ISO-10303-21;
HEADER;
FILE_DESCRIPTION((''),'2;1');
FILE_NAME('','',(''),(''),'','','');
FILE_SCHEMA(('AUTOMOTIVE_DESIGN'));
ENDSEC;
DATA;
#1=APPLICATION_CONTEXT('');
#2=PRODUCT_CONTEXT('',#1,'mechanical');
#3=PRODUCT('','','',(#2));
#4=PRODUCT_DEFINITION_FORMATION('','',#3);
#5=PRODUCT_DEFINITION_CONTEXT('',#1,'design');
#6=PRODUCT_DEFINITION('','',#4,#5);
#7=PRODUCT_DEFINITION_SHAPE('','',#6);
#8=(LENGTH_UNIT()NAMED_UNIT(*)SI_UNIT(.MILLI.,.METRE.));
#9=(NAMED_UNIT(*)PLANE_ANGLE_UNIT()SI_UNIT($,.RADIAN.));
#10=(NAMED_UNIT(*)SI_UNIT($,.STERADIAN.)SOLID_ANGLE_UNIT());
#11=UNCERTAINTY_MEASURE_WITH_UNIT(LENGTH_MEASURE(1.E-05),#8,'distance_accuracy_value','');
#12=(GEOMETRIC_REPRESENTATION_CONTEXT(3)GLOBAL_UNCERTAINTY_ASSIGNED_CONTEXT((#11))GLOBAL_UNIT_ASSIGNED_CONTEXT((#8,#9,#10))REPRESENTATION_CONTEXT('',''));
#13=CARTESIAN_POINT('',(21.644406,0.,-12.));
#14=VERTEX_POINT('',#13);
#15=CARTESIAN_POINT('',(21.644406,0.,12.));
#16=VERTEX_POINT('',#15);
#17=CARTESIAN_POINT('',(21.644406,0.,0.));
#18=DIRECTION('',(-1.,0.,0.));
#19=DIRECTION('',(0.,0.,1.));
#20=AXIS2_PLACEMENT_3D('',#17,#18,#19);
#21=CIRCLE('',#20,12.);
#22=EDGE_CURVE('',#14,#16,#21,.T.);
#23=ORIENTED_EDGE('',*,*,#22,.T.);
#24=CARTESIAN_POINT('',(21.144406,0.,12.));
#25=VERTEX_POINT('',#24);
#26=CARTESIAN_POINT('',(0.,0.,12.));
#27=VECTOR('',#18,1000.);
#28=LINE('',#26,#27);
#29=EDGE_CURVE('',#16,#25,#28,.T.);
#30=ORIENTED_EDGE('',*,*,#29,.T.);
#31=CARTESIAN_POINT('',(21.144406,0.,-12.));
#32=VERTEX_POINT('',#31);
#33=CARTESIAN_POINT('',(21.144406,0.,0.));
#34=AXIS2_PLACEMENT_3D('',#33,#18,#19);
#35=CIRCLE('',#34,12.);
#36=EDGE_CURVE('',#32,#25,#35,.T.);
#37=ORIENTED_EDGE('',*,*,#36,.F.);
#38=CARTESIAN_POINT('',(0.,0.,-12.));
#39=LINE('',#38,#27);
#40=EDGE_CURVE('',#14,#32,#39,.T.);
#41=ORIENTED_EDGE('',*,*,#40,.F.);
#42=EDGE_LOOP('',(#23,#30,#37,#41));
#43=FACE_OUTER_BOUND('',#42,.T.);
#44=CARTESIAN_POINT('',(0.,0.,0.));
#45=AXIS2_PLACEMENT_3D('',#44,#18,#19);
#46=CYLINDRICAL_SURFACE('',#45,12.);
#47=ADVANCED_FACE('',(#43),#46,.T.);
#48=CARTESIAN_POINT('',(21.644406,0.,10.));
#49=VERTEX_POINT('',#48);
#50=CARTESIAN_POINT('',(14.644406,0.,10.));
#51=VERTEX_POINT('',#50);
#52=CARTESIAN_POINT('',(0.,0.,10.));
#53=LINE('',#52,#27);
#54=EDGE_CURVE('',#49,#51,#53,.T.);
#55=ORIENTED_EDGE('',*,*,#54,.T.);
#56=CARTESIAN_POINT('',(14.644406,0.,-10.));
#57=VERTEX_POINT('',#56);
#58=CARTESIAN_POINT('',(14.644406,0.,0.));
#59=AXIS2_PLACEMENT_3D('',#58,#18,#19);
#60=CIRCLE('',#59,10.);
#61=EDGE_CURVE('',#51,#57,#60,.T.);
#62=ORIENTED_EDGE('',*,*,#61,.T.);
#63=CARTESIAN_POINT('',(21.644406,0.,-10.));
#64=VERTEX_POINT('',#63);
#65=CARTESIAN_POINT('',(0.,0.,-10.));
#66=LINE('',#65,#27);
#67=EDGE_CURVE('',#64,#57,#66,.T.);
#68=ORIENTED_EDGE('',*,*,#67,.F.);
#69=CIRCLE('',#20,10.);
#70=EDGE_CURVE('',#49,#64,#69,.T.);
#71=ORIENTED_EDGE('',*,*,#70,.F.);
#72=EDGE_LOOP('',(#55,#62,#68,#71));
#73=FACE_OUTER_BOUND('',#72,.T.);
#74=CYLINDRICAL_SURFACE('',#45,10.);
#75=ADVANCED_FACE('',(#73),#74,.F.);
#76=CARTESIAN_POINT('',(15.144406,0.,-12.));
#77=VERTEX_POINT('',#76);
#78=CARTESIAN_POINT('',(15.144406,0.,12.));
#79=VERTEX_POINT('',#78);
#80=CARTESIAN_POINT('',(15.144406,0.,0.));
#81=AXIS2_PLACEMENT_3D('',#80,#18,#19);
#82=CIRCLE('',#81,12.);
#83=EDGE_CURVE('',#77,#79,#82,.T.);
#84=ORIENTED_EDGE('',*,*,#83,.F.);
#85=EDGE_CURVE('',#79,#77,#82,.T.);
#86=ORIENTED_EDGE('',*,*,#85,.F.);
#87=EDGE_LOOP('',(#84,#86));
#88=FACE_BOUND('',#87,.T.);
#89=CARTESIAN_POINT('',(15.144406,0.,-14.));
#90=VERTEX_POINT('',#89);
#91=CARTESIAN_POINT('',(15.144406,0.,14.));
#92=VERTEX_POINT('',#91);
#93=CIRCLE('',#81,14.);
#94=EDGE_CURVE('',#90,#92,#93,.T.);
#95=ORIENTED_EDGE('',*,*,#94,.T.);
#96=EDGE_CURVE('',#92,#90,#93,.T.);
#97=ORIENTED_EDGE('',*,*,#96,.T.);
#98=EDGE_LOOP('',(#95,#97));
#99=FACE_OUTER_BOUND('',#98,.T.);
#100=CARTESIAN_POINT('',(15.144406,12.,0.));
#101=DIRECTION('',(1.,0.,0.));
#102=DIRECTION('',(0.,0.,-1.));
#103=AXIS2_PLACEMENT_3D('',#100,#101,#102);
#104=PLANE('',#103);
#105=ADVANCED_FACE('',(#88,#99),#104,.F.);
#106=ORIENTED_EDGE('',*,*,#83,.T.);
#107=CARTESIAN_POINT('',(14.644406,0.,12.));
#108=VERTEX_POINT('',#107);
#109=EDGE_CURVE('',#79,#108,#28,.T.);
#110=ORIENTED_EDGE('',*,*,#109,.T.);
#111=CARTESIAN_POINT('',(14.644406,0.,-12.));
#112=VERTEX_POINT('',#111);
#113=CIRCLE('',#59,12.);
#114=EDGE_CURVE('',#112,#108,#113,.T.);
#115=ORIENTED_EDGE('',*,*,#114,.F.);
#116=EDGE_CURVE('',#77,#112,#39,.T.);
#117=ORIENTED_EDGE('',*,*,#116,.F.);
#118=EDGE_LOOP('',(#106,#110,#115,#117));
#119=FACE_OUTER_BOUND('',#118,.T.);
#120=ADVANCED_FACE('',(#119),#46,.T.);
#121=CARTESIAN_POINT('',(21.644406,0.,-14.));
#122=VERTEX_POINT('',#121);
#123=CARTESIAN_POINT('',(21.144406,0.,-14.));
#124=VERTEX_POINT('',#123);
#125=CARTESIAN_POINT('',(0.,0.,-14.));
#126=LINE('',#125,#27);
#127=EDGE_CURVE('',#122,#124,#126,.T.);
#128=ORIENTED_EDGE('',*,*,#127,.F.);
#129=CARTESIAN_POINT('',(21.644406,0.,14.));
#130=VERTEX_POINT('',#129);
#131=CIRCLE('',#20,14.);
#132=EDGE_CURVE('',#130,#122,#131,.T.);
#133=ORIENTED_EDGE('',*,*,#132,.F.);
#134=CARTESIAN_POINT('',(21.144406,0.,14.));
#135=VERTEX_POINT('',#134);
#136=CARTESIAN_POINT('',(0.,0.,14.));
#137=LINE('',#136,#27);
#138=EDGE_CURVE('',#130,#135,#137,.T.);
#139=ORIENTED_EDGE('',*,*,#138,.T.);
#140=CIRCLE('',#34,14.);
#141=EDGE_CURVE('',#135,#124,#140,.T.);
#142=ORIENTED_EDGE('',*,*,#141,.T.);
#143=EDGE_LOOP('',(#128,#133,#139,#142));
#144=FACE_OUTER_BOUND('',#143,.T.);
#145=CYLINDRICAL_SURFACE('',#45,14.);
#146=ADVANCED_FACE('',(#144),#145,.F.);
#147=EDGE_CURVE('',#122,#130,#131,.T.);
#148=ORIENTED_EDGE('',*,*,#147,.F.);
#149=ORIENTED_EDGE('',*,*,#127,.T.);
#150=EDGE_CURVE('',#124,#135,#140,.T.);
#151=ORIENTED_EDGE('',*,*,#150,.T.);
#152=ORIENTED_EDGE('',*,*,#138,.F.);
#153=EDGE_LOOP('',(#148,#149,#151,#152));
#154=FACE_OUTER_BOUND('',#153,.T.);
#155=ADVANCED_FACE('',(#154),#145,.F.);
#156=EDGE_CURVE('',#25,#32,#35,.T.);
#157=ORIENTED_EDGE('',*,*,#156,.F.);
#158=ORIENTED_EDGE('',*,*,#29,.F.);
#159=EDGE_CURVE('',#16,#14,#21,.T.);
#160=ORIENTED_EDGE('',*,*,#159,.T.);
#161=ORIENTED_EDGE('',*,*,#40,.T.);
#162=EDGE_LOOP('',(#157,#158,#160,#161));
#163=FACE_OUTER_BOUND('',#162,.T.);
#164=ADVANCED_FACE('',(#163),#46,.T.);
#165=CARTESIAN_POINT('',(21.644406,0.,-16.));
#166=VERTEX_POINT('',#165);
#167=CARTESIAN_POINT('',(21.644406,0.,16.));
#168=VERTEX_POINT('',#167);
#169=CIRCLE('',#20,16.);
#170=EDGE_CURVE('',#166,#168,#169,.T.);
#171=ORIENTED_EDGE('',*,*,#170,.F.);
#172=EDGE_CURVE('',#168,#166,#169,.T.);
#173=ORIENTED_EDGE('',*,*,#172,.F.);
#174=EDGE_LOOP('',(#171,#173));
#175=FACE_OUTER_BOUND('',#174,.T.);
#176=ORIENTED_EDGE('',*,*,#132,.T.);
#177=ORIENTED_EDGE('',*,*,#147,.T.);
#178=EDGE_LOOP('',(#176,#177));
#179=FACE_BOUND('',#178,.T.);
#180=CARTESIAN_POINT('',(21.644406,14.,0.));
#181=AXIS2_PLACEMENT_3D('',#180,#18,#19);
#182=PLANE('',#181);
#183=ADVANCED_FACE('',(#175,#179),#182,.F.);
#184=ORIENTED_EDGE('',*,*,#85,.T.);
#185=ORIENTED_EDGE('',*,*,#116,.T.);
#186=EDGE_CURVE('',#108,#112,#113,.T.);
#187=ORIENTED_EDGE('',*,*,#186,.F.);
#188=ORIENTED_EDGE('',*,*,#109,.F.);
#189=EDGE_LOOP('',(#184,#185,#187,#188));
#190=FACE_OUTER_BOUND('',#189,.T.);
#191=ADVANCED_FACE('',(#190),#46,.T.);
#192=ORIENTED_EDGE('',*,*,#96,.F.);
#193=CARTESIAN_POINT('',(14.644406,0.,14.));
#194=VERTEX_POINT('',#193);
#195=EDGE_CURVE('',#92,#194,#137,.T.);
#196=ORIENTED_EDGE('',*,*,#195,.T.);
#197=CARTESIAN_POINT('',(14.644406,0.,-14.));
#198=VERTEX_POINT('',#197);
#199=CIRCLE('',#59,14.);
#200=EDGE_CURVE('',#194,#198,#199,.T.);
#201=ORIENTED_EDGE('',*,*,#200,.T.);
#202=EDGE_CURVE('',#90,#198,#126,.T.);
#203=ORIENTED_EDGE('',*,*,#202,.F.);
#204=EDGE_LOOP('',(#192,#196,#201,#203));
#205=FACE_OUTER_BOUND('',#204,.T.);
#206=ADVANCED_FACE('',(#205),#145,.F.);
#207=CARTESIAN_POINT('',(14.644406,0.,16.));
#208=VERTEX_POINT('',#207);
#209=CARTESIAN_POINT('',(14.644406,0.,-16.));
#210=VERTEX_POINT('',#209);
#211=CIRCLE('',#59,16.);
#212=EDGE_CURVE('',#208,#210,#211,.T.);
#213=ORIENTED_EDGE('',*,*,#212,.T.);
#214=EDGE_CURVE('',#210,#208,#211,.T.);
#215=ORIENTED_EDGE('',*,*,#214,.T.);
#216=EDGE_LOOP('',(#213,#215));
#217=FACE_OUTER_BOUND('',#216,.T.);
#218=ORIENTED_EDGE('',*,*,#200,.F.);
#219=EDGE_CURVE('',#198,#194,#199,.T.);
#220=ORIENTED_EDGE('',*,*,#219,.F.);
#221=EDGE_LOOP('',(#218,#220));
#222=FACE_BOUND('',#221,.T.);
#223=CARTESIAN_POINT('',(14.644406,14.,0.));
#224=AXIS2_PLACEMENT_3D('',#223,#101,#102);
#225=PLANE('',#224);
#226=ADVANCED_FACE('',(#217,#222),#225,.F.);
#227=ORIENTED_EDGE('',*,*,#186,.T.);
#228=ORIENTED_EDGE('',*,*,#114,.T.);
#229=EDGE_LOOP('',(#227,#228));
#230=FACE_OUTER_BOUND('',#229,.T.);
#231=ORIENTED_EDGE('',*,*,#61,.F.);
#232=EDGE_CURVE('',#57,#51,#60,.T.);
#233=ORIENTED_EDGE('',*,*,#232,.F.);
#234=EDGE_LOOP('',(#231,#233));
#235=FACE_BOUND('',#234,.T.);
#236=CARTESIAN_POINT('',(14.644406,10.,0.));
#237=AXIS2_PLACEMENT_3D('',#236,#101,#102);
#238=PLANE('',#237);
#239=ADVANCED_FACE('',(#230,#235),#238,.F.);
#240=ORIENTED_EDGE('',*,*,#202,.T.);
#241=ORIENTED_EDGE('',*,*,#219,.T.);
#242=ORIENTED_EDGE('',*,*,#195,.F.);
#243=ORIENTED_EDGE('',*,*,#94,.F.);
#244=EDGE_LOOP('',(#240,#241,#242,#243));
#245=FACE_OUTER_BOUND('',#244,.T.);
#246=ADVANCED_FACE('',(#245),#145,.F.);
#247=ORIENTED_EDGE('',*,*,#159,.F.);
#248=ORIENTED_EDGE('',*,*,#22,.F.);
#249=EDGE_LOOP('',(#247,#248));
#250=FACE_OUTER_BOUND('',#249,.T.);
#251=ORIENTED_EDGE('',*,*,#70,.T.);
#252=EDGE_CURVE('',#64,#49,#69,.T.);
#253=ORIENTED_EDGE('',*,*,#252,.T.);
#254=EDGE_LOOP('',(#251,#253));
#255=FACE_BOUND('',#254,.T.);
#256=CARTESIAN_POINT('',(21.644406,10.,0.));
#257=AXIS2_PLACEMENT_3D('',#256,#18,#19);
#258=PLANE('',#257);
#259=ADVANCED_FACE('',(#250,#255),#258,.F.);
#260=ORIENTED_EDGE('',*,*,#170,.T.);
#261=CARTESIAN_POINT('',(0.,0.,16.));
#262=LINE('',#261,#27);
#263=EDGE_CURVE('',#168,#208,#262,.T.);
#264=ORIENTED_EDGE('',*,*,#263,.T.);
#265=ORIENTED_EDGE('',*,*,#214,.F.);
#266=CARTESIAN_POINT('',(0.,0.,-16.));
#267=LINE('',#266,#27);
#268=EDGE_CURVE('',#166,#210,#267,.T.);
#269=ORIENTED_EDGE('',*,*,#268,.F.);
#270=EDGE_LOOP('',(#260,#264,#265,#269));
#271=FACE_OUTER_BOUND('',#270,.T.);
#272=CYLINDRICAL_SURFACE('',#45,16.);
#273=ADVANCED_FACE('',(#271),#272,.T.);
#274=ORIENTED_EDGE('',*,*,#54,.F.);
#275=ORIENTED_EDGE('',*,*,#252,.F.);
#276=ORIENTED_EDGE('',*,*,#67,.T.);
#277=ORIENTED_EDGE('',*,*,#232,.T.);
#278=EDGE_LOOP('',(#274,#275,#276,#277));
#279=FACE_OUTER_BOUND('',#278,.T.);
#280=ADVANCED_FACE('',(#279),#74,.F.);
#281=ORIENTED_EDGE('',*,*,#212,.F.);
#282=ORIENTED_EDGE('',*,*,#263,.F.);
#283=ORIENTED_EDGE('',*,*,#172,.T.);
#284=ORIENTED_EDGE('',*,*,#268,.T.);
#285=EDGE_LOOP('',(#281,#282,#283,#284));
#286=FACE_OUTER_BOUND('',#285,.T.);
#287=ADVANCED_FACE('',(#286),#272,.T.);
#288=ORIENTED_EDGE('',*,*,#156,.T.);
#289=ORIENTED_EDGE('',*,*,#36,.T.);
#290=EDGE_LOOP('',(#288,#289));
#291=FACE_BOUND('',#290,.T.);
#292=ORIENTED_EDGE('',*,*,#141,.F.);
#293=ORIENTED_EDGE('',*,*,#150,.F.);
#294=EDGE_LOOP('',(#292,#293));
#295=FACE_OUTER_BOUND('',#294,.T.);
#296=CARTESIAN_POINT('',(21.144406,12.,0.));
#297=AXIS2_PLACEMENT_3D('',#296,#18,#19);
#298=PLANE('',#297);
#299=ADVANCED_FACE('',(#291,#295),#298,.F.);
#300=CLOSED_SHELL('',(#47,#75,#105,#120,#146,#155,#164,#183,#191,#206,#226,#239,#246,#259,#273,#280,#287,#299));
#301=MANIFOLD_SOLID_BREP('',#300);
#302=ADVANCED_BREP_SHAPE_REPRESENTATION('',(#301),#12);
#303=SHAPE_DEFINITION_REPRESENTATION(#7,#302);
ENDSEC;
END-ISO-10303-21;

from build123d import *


with BuildPart() as part:
    # Sketch1 → Revolve1 (revolve)
    with BuildSketch(Plane.XY, mode=Mode.PRIVATE) as revolve1_sk:
        Polygon((14.644406169, 14), (14.644406169, 16), (21.644406169, 16), (21.644406169, 14), (21.144406169, 14), (21.144406169, 12), (21.644406169, 12), (21.644406169, 10), (14.644406169, 10), (14.644406169, 12), (15.144406169, 12), (15.144406169, 14), align=None)
    revolve(revolve1_sk.sketch.rotate(Axis((0, 0, 0), (1, 0, 0)), 90), axis=Axis((0, 0, 0), (1, 0, 0)))


solid = part.part
